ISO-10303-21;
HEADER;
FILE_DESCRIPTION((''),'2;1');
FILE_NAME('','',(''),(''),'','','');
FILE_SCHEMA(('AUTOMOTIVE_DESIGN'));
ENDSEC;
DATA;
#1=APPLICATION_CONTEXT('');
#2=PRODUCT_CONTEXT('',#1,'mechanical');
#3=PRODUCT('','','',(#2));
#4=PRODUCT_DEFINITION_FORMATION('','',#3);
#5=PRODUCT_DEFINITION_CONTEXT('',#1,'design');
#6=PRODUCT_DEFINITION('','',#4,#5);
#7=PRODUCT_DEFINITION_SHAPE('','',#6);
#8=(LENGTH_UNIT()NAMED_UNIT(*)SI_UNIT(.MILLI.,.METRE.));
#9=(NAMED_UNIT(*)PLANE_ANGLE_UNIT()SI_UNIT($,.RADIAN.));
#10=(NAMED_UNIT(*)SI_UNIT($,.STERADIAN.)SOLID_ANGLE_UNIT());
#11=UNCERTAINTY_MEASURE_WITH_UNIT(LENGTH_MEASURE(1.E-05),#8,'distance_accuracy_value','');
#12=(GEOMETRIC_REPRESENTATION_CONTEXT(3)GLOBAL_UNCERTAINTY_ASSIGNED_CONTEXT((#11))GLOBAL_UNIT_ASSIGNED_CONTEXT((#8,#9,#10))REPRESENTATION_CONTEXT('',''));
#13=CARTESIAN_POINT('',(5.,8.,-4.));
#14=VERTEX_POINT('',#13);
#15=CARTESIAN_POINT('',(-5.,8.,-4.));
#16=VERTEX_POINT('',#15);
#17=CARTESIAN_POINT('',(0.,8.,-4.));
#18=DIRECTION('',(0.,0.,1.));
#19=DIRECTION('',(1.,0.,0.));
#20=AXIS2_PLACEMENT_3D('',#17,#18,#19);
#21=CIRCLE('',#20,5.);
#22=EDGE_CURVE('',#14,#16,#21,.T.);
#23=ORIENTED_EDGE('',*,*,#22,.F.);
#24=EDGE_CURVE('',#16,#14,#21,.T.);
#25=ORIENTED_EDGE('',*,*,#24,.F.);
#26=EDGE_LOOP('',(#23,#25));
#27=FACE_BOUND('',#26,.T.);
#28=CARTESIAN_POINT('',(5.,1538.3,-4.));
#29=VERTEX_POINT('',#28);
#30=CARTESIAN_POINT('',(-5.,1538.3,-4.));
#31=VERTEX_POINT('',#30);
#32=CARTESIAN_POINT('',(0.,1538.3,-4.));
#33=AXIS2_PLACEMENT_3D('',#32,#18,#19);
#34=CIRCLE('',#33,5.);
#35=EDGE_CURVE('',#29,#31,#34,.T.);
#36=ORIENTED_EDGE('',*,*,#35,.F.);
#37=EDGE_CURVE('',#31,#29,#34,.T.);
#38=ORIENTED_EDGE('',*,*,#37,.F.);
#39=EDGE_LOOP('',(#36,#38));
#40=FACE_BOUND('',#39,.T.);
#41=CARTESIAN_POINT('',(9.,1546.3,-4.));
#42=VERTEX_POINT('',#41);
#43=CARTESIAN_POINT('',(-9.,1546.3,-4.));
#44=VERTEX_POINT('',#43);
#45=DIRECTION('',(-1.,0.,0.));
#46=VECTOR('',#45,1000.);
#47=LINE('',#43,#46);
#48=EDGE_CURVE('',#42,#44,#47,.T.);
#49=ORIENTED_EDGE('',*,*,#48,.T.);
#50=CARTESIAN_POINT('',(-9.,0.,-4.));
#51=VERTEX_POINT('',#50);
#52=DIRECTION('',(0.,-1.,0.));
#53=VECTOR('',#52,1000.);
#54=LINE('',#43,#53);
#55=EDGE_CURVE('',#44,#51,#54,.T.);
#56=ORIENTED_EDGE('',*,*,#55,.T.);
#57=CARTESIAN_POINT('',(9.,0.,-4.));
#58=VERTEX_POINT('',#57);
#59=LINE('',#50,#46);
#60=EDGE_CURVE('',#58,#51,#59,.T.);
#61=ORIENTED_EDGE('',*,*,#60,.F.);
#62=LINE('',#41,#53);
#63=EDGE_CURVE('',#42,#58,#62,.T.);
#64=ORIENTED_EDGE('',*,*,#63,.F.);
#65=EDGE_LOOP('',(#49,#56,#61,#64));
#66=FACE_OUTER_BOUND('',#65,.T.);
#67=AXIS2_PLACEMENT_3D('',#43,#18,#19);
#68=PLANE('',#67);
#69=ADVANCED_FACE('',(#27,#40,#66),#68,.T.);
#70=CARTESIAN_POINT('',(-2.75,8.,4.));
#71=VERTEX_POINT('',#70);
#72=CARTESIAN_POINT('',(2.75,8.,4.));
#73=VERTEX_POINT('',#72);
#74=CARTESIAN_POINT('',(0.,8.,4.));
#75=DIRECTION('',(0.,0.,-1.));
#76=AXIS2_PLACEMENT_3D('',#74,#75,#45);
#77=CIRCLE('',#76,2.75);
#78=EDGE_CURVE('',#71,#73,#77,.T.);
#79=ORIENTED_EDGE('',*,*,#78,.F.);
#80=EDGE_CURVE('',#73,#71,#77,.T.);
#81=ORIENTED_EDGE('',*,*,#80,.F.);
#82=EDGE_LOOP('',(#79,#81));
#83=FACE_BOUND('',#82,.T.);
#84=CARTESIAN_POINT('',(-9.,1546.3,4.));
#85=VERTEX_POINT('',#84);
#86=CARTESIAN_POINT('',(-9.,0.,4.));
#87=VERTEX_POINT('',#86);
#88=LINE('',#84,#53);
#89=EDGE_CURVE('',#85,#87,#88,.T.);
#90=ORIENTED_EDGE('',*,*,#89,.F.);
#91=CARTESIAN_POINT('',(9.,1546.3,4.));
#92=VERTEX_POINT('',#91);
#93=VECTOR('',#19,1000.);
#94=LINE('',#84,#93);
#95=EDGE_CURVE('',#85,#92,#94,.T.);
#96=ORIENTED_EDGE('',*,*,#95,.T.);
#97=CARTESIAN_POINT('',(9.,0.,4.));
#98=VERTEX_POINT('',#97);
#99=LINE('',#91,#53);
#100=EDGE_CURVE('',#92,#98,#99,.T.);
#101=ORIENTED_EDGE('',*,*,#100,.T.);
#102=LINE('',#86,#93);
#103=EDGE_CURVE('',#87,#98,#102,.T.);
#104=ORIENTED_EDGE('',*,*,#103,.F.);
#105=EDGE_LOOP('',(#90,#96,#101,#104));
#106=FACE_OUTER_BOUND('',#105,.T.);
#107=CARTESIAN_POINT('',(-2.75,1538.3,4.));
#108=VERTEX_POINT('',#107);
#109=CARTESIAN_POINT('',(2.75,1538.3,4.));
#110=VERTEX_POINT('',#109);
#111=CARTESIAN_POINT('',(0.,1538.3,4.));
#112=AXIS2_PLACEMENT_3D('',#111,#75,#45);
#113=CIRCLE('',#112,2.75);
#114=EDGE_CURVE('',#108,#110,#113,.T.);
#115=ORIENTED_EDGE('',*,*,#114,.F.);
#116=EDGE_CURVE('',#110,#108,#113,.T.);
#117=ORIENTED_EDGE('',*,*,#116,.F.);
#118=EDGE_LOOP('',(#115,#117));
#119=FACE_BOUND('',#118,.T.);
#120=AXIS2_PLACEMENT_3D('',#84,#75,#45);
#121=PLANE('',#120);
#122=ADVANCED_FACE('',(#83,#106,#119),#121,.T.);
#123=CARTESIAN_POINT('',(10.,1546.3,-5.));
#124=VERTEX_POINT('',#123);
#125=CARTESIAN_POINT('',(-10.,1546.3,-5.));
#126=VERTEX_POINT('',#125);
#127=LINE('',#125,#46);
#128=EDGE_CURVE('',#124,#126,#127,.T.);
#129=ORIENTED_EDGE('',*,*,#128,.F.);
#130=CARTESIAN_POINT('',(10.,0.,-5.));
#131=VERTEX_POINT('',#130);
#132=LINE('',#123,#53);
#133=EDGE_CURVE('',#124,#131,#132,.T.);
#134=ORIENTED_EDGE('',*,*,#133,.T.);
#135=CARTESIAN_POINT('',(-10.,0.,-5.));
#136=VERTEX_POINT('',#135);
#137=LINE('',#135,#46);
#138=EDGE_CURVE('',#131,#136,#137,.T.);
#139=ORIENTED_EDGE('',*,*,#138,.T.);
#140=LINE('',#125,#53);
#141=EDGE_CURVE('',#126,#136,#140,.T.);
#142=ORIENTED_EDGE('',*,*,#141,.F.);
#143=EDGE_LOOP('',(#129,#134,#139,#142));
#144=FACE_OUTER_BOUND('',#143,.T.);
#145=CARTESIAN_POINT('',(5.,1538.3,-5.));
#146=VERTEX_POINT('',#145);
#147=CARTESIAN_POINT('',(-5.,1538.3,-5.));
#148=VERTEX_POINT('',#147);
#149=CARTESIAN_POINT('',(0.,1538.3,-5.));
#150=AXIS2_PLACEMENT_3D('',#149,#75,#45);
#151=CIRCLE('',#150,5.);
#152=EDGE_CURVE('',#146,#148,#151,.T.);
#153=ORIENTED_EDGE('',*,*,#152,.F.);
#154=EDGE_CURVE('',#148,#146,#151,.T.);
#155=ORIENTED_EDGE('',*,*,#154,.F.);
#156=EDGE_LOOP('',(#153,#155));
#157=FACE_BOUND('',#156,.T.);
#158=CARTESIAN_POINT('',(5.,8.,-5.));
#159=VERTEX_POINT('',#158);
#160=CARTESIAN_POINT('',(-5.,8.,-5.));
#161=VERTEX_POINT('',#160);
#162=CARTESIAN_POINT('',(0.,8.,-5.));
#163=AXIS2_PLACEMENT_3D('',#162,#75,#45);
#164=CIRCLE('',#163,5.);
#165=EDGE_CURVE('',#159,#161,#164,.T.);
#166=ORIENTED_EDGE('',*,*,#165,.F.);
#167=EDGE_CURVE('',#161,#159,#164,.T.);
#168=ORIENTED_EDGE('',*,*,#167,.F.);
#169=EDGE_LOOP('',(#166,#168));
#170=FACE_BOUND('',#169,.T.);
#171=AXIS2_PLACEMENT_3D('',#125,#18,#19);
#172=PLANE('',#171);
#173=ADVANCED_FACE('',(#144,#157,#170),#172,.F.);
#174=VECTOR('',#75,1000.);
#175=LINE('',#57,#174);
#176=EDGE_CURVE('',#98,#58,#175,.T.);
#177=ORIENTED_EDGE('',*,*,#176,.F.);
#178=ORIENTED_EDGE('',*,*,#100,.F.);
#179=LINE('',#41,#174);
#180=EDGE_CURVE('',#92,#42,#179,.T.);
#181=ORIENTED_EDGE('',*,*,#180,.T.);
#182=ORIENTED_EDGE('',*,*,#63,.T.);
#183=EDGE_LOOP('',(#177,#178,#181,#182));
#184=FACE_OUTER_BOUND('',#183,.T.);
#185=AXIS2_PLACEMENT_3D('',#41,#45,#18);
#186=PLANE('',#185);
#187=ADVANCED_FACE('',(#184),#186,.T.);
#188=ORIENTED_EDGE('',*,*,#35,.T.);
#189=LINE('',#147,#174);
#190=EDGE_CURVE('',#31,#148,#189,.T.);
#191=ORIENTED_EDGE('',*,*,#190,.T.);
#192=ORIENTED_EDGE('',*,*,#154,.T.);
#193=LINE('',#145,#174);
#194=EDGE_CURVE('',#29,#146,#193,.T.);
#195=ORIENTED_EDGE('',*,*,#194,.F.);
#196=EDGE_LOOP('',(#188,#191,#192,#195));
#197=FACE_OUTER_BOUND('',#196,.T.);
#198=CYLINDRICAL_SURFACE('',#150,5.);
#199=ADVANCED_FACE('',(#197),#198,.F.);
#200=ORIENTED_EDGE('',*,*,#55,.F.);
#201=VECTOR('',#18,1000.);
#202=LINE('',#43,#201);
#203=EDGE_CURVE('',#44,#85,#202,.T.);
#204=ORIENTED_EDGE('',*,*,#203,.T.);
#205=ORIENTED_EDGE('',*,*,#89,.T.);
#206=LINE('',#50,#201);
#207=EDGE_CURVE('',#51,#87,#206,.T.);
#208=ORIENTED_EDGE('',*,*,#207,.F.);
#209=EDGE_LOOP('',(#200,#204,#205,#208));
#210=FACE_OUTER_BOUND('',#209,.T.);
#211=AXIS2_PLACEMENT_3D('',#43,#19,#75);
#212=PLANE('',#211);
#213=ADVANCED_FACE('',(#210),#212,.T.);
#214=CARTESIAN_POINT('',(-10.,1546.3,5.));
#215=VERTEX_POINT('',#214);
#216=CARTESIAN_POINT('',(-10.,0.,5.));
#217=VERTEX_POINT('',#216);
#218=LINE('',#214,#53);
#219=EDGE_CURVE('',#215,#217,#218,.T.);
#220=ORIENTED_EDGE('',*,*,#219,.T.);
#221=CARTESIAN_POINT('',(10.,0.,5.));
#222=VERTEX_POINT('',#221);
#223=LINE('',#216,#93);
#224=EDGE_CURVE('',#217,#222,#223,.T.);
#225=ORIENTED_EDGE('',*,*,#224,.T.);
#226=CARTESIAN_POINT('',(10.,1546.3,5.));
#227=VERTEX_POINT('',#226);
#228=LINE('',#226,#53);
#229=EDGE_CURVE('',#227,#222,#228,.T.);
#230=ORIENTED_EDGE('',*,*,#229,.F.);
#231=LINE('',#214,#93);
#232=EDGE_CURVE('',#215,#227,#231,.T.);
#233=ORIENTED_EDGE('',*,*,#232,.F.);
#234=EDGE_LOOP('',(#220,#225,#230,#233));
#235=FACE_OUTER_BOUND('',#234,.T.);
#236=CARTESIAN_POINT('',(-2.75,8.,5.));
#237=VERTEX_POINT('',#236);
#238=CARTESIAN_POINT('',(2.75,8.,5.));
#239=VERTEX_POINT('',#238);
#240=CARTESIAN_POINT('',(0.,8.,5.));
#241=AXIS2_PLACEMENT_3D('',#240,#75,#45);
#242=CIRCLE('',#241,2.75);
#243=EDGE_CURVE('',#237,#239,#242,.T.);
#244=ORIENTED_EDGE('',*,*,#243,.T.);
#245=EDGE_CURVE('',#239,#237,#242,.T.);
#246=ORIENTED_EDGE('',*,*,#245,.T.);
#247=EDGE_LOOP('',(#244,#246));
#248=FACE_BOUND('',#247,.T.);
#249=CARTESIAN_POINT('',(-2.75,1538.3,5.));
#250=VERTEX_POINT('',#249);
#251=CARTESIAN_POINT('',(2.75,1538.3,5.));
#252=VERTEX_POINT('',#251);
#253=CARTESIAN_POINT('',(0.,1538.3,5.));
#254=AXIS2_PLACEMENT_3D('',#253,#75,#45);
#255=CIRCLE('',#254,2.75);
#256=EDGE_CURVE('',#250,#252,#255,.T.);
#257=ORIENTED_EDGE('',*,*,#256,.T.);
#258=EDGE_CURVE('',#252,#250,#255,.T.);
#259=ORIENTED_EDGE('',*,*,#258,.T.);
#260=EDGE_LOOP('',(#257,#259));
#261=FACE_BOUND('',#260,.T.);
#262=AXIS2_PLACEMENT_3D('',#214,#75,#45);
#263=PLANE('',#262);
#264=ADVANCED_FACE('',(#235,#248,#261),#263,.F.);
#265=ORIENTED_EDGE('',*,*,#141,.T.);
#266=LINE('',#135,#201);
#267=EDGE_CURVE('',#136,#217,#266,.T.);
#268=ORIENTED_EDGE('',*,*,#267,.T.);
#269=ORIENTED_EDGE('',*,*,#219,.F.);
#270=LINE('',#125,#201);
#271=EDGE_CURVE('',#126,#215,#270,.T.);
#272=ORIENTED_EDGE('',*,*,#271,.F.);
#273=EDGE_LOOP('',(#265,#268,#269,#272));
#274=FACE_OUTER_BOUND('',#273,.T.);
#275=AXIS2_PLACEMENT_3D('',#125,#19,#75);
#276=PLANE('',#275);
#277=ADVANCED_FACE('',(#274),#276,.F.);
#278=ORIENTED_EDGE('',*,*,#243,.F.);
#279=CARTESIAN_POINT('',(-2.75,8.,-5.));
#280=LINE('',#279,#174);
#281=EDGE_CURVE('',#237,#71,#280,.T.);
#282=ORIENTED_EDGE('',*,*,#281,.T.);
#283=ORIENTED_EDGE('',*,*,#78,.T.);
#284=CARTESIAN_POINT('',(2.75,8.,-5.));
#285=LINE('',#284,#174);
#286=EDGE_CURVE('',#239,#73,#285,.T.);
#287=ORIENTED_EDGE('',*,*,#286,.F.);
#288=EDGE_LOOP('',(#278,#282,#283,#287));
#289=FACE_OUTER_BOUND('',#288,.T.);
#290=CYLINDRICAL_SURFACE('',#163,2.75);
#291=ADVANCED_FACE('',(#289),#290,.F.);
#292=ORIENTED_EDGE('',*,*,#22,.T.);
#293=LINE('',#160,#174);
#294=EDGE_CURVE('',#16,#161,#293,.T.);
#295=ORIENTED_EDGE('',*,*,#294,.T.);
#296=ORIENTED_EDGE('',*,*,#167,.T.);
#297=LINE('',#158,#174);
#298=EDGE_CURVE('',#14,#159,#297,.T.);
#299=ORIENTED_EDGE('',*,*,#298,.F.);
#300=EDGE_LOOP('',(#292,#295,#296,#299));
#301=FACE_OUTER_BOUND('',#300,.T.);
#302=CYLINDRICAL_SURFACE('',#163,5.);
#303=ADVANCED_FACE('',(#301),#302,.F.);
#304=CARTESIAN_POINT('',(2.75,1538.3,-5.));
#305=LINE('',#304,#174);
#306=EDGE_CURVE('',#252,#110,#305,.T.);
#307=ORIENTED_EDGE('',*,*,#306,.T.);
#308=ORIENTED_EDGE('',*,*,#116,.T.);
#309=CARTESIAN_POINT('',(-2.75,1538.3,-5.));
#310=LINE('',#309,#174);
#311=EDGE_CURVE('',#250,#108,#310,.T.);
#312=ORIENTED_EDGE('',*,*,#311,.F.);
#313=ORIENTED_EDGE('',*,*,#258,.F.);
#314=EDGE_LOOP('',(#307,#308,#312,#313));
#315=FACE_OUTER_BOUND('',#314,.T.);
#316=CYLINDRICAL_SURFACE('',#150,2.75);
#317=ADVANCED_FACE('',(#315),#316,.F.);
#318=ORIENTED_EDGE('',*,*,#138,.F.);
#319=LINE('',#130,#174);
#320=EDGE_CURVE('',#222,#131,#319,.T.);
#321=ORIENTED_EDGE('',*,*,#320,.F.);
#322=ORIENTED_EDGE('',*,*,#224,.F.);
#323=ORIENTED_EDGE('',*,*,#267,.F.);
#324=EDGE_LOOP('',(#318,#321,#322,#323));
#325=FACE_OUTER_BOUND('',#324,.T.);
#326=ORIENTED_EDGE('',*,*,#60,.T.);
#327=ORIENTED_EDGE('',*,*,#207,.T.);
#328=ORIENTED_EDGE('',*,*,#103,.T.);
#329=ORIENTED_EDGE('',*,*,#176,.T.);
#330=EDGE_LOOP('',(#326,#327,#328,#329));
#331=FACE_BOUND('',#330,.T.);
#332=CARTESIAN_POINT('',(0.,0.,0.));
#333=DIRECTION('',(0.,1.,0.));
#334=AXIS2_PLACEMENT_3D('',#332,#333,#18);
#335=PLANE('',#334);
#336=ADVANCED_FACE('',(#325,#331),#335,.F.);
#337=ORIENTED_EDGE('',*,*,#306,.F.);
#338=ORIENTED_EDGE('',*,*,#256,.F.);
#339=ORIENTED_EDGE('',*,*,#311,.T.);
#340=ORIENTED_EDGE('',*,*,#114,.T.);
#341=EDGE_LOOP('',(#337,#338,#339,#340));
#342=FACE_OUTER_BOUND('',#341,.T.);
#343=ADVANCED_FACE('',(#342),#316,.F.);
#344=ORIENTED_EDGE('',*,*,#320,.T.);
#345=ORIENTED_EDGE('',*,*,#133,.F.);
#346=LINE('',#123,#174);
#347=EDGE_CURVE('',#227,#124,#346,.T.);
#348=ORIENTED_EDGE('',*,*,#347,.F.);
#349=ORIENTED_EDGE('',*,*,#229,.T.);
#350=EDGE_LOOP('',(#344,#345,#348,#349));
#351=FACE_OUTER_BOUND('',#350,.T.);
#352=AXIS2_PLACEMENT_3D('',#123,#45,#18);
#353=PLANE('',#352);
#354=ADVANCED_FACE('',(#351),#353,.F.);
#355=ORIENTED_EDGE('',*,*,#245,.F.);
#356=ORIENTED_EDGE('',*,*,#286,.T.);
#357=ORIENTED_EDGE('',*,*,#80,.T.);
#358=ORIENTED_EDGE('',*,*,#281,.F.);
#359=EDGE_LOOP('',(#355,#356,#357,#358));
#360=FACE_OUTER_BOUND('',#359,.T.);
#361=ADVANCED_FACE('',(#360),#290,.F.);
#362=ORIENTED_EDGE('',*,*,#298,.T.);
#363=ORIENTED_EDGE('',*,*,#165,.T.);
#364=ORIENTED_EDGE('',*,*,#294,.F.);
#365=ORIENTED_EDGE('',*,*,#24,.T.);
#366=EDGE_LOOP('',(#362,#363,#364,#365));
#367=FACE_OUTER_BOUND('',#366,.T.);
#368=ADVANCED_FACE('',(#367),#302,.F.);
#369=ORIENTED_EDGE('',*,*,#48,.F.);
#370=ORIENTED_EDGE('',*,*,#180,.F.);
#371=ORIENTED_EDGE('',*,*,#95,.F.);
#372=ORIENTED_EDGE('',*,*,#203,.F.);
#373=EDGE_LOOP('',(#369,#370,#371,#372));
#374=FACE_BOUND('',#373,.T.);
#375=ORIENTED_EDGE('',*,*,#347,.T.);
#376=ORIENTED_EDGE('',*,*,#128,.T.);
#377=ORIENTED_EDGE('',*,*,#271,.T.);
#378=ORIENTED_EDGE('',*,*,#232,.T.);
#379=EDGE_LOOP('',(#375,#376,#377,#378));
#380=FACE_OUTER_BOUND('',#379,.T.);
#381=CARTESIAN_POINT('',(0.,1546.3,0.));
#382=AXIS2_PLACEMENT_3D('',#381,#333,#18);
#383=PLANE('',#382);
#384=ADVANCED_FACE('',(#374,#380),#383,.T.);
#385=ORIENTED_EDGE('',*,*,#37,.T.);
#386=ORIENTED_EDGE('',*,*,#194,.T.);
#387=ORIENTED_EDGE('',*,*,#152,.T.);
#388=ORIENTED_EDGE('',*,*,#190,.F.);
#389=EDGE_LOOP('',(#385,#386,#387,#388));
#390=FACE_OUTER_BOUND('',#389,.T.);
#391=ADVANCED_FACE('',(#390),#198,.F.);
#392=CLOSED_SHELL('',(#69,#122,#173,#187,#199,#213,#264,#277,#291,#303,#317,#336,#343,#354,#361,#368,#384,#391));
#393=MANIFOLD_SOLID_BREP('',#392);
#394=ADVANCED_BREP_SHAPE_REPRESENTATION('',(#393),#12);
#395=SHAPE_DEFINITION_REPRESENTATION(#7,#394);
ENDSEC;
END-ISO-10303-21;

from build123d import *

# Parameters (mm, degrees)
SKETCH_2_W                = 20
SKETCH_2_H                = 10
SKETCH_2_W_2              = 18
SKETCH_2_H_2              = 8
EXTRUDE_1_DEPTH           = 1546.3
HOLE_WIZARD_1_D           = 5.5
HOLE_WIZARD_1_CBORE_D     = 10
HOLE_WIZARD_1_CBORE_DEPTH = 5.7


with BuildPart() as part:
    # 草图2 → 凸台-拉伸1 (new body)
    with BuildSketch(Plane(origin=(0, 0, 0), x_dir=(1, 0, 0), z_dir=(0, 1, 0))):
        Rectangle(SKETCH_2_W, SKETCH_2_H)
        Rectangle(SKETCH_2_W_2, SKETCH_2_H_2, mode=Mode.SUBTRACT)
    extrude(amount=EXTRUDE_1_DEPTH)

    # 打孔尺寸(%根据)内六角圆柱头螺钉的类型1 (through all)
    with Locations(Plane(origin=(0, 0, -5), x_dir=(-1, 0, 0), z_dir=(0, 0, -1))):
        with Locations((0, 1538.3), (0, 8)):
            CounterBoreHole(HOLE_WIZARD_1_D / 2, HOLE_WIZARD_1_CBORE_D / 2, HOLE_WIZARD_1_CBORE_DEPTH)


solid = part.part
